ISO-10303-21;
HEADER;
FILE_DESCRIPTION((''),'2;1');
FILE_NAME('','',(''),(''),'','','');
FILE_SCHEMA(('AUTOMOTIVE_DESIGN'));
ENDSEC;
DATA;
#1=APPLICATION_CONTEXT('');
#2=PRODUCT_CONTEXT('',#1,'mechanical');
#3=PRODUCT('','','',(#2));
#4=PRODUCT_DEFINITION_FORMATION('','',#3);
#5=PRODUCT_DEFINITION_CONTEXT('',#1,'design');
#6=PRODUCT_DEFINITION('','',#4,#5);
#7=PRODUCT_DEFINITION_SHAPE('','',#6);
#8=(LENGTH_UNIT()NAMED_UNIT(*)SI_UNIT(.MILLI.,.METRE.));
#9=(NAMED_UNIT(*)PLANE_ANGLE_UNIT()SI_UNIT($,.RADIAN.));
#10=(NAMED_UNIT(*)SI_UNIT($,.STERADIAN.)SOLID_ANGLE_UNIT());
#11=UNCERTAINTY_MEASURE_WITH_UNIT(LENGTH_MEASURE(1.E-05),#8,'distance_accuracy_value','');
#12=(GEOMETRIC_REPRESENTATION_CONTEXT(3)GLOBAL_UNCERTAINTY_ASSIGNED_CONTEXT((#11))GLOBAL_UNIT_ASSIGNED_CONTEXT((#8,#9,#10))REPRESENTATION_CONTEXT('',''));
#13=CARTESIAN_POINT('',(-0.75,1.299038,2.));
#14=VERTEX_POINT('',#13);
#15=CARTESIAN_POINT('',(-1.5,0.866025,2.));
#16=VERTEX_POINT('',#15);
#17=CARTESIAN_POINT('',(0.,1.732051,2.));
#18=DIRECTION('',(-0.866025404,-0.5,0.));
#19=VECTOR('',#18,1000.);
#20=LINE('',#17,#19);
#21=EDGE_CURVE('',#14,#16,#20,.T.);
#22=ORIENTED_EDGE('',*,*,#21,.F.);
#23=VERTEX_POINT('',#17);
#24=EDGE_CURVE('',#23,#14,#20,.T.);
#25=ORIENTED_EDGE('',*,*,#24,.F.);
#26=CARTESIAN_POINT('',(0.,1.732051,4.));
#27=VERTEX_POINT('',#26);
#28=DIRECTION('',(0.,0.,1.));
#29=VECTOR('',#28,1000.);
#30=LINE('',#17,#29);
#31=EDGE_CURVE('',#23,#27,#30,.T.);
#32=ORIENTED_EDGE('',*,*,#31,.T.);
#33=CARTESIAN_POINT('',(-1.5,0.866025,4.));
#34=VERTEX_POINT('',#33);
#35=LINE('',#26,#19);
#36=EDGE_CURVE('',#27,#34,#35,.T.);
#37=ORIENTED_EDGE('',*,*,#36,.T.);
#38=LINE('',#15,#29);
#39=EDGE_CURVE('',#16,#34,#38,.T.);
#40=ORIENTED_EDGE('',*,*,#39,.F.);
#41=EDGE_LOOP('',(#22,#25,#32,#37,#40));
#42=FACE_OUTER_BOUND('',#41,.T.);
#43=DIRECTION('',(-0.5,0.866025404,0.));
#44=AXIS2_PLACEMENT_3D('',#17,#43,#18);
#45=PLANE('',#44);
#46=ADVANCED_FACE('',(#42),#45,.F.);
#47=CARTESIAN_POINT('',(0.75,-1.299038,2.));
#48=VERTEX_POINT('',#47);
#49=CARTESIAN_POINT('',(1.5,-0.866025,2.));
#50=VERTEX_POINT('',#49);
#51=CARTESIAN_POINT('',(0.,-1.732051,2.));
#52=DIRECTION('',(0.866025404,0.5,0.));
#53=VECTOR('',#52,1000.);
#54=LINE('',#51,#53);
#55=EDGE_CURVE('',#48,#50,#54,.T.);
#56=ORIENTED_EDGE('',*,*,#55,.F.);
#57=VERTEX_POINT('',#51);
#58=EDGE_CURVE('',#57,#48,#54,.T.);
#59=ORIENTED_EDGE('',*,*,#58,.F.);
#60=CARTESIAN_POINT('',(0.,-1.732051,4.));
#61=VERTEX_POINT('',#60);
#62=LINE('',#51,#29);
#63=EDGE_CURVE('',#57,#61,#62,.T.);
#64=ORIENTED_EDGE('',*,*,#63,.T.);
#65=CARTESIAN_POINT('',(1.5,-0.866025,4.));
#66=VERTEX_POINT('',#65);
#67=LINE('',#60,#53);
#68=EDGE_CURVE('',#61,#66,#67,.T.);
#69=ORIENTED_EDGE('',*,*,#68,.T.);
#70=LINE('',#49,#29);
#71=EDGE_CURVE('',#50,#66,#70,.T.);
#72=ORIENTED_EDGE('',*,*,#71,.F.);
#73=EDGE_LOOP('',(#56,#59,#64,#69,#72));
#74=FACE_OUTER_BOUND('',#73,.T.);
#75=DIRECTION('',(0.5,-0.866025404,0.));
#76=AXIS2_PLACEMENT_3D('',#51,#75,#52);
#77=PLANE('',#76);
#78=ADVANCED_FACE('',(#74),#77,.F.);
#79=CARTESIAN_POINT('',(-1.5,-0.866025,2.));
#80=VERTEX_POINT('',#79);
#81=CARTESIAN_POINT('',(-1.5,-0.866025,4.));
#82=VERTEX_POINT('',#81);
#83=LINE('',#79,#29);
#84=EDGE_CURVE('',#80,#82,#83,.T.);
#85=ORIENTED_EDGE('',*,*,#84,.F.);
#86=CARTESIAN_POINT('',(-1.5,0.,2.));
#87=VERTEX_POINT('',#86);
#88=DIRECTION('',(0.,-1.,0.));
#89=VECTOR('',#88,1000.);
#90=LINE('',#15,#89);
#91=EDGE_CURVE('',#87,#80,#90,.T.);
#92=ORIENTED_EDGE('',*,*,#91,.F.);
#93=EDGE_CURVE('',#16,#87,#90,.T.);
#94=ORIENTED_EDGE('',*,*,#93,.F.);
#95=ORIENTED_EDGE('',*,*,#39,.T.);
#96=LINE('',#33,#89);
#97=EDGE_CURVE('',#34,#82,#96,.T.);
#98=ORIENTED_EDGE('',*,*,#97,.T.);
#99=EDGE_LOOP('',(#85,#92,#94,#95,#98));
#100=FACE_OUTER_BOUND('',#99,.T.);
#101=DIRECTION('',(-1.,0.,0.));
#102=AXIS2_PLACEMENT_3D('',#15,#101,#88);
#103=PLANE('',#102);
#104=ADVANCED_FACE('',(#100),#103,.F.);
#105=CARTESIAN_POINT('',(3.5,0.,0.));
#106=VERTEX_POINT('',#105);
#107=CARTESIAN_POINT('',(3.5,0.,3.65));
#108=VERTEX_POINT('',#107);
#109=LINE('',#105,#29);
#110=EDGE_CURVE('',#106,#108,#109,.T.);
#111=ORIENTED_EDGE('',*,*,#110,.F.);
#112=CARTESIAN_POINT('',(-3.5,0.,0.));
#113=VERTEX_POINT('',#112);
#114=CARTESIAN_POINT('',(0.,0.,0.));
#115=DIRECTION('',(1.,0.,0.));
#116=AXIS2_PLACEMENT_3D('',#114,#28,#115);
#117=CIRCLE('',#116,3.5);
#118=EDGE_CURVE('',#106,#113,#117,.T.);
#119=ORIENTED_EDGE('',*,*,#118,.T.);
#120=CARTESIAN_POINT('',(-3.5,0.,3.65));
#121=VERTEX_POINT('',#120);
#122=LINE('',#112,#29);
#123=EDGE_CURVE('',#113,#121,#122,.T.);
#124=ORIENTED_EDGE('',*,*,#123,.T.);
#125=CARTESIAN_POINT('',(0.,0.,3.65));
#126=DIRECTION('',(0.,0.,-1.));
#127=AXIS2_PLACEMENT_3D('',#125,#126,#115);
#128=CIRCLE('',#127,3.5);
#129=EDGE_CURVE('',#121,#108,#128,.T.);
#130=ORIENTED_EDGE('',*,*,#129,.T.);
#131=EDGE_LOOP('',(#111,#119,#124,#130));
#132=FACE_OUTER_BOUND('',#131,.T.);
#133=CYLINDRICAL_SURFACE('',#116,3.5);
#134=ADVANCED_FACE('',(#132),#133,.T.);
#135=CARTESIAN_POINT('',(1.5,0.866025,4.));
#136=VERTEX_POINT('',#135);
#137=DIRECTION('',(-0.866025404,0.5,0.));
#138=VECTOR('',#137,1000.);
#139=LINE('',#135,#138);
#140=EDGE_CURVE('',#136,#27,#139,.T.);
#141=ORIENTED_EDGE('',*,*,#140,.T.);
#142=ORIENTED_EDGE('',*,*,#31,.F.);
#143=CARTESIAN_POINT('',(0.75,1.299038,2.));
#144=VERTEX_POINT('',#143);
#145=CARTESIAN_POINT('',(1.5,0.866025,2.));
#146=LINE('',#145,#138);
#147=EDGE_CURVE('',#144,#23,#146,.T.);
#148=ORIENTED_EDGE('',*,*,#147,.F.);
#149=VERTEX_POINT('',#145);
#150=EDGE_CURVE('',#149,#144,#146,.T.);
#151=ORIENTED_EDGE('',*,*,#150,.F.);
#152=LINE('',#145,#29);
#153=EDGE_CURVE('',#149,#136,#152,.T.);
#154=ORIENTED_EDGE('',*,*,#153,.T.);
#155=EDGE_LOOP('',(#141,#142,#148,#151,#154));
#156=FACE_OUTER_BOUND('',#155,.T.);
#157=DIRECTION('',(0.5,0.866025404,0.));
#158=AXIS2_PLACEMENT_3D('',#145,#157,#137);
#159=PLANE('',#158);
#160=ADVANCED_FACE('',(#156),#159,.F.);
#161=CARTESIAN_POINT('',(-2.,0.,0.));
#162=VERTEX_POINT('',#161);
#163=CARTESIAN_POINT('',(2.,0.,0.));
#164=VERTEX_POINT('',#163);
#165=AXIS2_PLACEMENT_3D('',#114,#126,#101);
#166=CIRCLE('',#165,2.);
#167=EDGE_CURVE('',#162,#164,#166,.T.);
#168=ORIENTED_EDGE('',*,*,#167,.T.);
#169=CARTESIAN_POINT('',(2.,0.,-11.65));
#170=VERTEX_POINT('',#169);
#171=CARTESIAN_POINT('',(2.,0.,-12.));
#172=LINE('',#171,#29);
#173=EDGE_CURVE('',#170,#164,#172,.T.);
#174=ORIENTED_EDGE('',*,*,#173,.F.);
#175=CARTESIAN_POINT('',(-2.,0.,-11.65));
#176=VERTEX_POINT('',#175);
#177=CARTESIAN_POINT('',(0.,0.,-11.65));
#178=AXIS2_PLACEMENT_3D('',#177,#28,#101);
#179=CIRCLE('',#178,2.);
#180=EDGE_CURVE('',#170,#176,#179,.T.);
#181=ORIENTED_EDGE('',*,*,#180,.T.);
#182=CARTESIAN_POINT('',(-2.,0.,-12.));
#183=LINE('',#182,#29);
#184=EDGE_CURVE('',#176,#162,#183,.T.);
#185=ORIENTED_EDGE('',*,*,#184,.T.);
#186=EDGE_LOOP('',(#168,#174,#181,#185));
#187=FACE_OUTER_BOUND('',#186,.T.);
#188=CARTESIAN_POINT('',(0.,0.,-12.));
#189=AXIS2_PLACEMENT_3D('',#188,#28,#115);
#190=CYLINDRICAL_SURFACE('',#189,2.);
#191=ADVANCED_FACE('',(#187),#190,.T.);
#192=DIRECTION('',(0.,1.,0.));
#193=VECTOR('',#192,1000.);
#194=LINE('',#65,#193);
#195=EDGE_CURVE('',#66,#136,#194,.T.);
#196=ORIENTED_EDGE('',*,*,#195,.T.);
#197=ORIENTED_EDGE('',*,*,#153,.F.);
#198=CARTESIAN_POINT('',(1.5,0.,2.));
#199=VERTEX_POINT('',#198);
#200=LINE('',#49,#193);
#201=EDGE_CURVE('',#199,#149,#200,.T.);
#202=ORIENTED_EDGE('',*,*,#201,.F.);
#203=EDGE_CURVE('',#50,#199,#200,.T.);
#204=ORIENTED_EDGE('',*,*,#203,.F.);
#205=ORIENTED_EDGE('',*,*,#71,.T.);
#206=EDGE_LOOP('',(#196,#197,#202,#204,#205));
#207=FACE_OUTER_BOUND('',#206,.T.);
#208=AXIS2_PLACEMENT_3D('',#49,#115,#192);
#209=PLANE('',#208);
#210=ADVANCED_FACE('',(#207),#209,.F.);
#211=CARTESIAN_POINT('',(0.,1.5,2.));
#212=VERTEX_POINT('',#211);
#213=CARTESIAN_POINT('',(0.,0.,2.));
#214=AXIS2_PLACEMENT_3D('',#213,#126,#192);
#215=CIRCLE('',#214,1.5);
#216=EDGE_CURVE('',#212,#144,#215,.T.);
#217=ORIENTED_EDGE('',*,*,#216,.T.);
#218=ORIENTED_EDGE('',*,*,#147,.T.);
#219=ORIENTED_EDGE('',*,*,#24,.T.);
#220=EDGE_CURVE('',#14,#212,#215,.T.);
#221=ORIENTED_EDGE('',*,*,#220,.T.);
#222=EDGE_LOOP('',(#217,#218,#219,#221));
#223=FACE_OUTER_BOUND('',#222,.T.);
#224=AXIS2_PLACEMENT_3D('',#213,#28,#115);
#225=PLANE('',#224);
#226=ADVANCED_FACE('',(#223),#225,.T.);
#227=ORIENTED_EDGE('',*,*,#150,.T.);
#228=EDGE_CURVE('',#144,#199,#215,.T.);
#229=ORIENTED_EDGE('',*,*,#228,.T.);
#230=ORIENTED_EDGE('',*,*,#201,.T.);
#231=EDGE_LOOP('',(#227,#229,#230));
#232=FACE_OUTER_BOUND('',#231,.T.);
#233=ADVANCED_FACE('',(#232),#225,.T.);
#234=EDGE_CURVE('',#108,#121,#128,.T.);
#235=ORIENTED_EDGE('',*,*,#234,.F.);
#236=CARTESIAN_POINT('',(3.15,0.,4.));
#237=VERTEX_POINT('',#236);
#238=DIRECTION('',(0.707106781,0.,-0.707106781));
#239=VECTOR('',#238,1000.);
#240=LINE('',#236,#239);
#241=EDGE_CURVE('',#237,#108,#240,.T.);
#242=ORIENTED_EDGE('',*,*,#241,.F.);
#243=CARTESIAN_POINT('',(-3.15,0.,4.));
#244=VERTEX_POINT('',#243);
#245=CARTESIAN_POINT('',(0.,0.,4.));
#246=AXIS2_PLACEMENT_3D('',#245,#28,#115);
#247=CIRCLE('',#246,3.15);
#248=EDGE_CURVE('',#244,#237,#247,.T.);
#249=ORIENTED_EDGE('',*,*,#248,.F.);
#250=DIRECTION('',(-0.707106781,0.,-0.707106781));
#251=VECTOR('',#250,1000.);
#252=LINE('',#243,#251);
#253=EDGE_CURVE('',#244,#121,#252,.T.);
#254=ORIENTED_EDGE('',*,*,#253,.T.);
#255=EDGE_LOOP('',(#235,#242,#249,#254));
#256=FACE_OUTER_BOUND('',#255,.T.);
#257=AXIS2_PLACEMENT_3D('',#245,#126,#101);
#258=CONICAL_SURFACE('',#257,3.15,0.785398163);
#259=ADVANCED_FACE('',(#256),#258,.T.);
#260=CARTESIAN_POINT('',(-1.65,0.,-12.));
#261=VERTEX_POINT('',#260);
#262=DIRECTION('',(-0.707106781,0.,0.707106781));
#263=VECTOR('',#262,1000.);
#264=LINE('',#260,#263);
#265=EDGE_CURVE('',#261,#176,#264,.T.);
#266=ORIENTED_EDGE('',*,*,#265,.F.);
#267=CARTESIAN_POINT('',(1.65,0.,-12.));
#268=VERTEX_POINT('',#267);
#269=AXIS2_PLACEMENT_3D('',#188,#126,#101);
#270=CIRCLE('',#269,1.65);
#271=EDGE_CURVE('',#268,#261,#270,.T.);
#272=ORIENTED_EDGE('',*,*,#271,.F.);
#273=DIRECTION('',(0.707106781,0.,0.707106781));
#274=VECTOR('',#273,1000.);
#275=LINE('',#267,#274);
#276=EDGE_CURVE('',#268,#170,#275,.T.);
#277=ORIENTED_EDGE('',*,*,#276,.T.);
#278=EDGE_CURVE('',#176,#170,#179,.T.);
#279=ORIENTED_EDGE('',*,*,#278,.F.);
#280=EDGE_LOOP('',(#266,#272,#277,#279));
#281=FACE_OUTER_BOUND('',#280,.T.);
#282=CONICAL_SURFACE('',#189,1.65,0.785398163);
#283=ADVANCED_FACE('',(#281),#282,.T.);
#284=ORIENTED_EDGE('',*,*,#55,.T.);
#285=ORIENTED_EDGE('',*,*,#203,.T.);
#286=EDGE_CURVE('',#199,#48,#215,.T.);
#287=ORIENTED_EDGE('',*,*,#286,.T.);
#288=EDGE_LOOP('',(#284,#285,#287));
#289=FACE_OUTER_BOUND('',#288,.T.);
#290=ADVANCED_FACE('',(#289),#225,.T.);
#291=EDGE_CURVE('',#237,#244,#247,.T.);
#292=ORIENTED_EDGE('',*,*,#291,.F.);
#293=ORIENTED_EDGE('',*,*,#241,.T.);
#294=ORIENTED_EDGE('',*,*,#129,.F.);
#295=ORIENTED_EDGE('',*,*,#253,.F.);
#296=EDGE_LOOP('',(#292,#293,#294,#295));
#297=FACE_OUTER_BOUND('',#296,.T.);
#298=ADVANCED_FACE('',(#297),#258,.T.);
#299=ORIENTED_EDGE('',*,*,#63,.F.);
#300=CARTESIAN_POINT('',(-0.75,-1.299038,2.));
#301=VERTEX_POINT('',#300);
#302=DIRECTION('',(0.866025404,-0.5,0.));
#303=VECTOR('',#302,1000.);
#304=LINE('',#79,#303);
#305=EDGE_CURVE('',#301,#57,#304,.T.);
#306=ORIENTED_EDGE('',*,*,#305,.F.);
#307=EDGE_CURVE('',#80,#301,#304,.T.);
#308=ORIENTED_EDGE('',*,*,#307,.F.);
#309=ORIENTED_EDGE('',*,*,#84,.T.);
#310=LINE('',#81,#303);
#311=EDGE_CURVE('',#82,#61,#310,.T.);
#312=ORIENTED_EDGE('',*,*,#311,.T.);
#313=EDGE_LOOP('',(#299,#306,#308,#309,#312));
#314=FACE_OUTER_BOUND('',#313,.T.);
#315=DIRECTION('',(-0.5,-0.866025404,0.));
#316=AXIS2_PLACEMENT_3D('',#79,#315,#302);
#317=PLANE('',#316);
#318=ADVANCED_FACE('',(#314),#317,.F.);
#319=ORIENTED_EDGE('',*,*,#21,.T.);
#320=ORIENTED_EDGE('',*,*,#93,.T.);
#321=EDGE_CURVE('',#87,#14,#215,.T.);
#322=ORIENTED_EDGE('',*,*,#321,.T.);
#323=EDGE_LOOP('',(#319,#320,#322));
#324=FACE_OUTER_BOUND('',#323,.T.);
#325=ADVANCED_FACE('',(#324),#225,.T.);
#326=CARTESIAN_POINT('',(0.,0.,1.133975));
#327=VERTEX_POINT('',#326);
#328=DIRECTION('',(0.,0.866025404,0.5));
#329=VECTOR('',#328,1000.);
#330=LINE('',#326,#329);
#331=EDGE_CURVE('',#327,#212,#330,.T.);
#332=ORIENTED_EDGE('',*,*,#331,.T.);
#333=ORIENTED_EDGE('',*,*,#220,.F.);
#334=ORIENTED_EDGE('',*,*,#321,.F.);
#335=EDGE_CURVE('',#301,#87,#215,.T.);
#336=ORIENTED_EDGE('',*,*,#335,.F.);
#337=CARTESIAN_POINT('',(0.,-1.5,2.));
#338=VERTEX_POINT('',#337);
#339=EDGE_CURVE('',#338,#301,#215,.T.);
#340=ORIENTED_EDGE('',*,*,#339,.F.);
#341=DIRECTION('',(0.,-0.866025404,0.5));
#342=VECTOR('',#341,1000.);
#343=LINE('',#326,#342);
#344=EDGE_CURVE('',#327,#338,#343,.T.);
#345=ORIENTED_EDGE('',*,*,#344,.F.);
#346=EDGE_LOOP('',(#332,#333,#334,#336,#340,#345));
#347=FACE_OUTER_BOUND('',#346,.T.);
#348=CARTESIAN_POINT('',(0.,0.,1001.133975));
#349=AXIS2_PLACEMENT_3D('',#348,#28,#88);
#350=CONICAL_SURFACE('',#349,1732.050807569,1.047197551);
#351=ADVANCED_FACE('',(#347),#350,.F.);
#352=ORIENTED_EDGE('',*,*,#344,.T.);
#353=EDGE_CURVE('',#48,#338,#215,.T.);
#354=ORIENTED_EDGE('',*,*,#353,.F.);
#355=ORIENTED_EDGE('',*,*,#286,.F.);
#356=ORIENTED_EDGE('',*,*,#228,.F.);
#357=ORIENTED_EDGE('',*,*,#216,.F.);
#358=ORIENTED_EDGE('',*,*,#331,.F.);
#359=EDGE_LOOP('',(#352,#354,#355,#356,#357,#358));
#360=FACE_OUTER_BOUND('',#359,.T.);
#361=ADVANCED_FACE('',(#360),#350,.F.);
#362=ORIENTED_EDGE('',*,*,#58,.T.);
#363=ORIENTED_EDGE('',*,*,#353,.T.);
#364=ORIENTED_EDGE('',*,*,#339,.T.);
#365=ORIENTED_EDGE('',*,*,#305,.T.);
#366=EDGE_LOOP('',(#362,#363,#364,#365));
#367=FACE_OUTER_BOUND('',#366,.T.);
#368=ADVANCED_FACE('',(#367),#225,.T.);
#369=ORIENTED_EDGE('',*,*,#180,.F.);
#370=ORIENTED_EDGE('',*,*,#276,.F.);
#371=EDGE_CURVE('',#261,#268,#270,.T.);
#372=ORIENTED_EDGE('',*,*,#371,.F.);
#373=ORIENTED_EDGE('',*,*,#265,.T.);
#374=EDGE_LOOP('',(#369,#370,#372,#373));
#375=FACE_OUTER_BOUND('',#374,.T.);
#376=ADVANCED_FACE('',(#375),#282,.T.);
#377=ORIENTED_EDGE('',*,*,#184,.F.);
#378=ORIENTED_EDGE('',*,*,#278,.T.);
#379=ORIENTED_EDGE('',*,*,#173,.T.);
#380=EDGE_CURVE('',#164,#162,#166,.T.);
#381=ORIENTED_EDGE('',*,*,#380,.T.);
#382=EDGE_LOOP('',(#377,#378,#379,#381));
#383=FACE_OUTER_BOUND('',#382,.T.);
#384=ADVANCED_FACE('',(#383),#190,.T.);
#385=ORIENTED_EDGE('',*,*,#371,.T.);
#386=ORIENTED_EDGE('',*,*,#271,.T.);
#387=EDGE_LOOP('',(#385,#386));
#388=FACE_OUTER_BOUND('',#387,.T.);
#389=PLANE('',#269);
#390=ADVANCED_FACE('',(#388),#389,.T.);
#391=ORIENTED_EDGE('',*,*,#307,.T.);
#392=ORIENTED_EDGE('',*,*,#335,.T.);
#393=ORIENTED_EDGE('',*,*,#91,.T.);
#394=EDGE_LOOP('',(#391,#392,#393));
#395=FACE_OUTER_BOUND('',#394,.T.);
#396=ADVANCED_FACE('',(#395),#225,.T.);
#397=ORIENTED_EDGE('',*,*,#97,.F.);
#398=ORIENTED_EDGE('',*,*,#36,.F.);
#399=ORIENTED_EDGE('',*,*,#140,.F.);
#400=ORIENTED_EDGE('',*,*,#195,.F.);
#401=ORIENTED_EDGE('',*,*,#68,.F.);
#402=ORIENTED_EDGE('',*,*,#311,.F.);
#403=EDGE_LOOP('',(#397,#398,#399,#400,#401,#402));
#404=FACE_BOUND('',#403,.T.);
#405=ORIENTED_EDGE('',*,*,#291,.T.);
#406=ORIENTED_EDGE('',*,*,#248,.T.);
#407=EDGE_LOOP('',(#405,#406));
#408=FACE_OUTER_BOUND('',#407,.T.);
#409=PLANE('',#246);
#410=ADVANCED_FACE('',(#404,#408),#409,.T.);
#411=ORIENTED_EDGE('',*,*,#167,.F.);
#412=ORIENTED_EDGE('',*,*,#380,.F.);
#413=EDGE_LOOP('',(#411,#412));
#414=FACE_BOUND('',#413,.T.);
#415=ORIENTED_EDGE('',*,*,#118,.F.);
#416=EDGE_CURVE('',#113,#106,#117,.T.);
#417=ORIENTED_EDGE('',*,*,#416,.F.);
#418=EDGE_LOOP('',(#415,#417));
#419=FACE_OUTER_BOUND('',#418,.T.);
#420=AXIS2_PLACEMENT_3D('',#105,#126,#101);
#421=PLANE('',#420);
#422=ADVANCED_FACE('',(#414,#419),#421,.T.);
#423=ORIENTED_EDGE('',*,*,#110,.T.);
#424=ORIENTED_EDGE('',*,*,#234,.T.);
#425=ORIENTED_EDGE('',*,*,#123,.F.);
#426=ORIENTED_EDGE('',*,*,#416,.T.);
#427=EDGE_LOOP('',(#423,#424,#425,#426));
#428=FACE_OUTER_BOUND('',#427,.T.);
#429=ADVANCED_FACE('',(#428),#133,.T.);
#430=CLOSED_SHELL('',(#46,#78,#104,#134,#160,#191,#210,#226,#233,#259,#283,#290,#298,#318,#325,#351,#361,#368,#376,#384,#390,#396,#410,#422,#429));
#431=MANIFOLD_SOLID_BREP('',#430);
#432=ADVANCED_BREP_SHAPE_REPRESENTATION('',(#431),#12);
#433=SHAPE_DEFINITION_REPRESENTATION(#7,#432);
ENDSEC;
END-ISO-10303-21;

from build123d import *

# Parameters (mm, degrees)
SKETCH_1_W          = 3.5
SKETCH_1_H          = 4
SKETCH_2_R          = 2
EXTRUDE_1_DEPTH     = 12
CUT_EXTRUDE_1_DEPTH = 2
CHAMFER_1_SIZE      = 0.35


with BuildPart() as part:
    # 草图1 → 旋转1 (revolve)
    with BuildSketch(Plane(origin=(0, 0, 0), x_dir=(1, 0, 0), z_dir=(0, 1, 0))):
        with Locations((1.75, -2)):
            Rectangle(SKETCH_1_W, SKETCH_1_H)
    revolve(axis=Axis((0, 0, 0), (0, 0, 1)))

    # 草图2 → 凸台-拉伸1 (add)
    with BuildSketch(Plane(origin=(0, 0, 0), x_dir=(-1, 0, 0), z_dir=(0, 0, -1))):
        Circle(SKETCH_2_R)
    extrude(amount=EXTRUDE_1_DEPTH)

    # 草图3 → 切除-拉伸1 (cut)
    with BuildSketch(Plane.XY.offset(4)):
        Polygon((1.5, -0.866025404), (1.5, 0.866025404), (0, 1.732050808), (-1.5, 0.866025404), (-1.5, -0.866025404), (0, -1.732050808), align=None)
    extrude(amount=-CUT_EXTRUDE_1_DEPTH, mode=Mode.SUBTRACT)

    # 草图4 → 切除-旋转1 (revolve, cut)
    with BuildSketch(Plane.XZ, mode=Mode.PRIVATE) as cut_revolve_1_sk:
        Polygon((1.5, 2), (0, 2), (0, 1.133974596), align=None)
    revolve(cut_revolve_1_sk.sketch.rotate(Axis((0, 0, 2), (0, 0, -1)), 90), axis=Axis((0, 0, 2), (0, 0, -1)), mode=Mode.SUBTRACT)

    # 倒角1
    chamfer_1_edges = [part.edges().sort_by_distance(p)[0] for p in [
        (-3.5, 0, 4),
        (2, 0, -12),
    ]]
    chamfer(chamfer_1_edges, length=CHAMFER_1_SIZE)


solid = part.part
